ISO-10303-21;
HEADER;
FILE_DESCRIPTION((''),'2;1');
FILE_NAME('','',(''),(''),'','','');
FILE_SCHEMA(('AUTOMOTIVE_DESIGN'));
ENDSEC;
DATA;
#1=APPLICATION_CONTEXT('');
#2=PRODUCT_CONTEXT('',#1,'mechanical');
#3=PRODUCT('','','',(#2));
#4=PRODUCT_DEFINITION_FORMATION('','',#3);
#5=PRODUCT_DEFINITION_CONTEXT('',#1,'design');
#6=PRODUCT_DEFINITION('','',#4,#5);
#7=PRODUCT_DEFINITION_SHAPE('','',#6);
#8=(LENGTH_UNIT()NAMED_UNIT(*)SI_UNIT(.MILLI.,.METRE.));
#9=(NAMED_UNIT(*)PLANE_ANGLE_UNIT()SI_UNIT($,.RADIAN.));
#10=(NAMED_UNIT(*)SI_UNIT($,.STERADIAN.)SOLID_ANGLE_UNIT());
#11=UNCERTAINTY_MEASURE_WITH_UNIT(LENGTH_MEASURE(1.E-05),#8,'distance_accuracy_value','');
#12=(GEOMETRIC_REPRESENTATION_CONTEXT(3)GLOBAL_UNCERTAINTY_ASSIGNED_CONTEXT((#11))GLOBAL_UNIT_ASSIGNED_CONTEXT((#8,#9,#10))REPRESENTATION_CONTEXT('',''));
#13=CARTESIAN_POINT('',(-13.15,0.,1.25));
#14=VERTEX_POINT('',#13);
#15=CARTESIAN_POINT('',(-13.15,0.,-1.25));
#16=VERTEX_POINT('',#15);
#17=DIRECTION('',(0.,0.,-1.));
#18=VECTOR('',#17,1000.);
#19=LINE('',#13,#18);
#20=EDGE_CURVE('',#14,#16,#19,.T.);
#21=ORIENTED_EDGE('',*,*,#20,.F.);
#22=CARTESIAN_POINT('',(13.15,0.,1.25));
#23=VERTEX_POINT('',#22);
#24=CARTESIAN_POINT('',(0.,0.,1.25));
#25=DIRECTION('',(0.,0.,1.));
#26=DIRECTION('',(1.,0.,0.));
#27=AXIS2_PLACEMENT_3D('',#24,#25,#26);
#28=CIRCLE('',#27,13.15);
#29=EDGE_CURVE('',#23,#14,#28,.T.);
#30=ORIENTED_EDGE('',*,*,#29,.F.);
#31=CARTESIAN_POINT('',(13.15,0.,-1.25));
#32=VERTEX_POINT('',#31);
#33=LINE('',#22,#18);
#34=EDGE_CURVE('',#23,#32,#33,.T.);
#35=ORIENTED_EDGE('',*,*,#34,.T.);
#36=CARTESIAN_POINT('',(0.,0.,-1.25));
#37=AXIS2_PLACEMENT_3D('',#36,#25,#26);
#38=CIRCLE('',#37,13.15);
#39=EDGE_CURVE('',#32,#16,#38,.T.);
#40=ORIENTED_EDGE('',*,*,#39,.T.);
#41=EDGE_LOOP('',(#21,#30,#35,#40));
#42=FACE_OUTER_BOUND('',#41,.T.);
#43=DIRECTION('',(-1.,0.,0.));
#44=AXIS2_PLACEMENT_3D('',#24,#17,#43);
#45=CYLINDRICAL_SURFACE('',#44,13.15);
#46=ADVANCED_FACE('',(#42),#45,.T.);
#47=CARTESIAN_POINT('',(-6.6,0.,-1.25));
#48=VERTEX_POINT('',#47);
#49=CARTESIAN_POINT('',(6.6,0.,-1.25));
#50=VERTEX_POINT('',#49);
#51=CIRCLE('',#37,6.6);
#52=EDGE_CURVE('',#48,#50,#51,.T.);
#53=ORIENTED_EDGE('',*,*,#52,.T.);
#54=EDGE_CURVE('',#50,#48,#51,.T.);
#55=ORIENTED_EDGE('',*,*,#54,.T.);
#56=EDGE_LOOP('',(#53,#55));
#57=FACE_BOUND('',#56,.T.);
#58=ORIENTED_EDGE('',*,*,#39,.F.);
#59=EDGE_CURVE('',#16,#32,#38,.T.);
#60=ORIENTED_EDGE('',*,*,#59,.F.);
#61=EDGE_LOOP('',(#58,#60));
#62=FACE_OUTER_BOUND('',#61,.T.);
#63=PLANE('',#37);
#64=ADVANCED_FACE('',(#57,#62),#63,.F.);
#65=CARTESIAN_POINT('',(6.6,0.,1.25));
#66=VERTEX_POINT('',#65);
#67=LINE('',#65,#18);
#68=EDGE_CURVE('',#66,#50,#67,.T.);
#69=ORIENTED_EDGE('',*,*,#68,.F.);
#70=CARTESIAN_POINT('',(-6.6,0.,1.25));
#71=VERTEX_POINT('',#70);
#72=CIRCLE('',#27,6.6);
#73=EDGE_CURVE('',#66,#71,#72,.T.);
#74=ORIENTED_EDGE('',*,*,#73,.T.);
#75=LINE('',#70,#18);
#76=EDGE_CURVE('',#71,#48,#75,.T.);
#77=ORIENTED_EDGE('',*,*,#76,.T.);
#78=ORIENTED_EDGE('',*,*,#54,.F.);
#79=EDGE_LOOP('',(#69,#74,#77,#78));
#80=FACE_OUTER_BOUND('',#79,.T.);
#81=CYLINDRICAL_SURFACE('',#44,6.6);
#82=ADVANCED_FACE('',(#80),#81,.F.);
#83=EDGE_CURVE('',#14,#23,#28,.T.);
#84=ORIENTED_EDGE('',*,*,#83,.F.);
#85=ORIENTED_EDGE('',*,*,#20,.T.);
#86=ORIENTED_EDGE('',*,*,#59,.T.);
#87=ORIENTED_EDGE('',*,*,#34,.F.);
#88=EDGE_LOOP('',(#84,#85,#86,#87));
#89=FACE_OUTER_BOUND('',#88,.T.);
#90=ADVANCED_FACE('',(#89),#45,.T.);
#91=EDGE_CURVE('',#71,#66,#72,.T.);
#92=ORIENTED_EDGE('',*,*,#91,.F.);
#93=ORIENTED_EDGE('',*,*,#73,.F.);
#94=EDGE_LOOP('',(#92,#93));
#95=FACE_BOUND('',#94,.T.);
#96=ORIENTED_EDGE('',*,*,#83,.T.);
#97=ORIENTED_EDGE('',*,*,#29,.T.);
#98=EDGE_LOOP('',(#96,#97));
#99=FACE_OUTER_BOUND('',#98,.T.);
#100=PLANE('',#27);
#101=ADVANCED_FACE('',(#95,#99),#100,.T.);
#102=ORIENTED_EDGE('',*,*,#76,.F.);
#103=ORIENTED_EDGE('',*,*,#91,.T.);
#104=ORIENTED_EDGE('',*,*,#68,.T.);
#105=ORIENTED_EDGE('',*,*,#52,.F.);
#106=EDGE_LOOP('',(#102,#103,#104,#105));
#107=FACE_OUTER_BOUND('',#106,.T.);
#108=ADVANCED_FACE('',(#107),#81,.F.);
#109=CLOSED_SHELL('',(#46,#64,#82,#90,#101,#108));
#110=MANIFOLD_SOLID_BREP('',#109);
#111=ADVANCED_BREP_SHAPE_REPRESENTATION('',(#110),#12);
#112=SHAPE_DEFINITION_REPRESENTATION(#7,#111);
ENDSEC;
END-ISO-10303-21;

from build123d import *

# Parameters (mm, degrees)
SKETCH1_R           = 13.15
SKETCH1_R_2         = 6.6
BOSS_EXTRUDE1_DEPTH = 1.25


with BuildPart() as part:
    # Sketch1 → Boss-Extrude1 (new, symmetric)
    with BuildSketch(Plane.XY):
        Circle(SKETCH1_R)
        Circle(SKETCH1_R_2, mode=Mode.SUBTRACT)
    extrude(amount=BOSS_EXTRUDE1_DEPTH, both=True)


solid = part.part
